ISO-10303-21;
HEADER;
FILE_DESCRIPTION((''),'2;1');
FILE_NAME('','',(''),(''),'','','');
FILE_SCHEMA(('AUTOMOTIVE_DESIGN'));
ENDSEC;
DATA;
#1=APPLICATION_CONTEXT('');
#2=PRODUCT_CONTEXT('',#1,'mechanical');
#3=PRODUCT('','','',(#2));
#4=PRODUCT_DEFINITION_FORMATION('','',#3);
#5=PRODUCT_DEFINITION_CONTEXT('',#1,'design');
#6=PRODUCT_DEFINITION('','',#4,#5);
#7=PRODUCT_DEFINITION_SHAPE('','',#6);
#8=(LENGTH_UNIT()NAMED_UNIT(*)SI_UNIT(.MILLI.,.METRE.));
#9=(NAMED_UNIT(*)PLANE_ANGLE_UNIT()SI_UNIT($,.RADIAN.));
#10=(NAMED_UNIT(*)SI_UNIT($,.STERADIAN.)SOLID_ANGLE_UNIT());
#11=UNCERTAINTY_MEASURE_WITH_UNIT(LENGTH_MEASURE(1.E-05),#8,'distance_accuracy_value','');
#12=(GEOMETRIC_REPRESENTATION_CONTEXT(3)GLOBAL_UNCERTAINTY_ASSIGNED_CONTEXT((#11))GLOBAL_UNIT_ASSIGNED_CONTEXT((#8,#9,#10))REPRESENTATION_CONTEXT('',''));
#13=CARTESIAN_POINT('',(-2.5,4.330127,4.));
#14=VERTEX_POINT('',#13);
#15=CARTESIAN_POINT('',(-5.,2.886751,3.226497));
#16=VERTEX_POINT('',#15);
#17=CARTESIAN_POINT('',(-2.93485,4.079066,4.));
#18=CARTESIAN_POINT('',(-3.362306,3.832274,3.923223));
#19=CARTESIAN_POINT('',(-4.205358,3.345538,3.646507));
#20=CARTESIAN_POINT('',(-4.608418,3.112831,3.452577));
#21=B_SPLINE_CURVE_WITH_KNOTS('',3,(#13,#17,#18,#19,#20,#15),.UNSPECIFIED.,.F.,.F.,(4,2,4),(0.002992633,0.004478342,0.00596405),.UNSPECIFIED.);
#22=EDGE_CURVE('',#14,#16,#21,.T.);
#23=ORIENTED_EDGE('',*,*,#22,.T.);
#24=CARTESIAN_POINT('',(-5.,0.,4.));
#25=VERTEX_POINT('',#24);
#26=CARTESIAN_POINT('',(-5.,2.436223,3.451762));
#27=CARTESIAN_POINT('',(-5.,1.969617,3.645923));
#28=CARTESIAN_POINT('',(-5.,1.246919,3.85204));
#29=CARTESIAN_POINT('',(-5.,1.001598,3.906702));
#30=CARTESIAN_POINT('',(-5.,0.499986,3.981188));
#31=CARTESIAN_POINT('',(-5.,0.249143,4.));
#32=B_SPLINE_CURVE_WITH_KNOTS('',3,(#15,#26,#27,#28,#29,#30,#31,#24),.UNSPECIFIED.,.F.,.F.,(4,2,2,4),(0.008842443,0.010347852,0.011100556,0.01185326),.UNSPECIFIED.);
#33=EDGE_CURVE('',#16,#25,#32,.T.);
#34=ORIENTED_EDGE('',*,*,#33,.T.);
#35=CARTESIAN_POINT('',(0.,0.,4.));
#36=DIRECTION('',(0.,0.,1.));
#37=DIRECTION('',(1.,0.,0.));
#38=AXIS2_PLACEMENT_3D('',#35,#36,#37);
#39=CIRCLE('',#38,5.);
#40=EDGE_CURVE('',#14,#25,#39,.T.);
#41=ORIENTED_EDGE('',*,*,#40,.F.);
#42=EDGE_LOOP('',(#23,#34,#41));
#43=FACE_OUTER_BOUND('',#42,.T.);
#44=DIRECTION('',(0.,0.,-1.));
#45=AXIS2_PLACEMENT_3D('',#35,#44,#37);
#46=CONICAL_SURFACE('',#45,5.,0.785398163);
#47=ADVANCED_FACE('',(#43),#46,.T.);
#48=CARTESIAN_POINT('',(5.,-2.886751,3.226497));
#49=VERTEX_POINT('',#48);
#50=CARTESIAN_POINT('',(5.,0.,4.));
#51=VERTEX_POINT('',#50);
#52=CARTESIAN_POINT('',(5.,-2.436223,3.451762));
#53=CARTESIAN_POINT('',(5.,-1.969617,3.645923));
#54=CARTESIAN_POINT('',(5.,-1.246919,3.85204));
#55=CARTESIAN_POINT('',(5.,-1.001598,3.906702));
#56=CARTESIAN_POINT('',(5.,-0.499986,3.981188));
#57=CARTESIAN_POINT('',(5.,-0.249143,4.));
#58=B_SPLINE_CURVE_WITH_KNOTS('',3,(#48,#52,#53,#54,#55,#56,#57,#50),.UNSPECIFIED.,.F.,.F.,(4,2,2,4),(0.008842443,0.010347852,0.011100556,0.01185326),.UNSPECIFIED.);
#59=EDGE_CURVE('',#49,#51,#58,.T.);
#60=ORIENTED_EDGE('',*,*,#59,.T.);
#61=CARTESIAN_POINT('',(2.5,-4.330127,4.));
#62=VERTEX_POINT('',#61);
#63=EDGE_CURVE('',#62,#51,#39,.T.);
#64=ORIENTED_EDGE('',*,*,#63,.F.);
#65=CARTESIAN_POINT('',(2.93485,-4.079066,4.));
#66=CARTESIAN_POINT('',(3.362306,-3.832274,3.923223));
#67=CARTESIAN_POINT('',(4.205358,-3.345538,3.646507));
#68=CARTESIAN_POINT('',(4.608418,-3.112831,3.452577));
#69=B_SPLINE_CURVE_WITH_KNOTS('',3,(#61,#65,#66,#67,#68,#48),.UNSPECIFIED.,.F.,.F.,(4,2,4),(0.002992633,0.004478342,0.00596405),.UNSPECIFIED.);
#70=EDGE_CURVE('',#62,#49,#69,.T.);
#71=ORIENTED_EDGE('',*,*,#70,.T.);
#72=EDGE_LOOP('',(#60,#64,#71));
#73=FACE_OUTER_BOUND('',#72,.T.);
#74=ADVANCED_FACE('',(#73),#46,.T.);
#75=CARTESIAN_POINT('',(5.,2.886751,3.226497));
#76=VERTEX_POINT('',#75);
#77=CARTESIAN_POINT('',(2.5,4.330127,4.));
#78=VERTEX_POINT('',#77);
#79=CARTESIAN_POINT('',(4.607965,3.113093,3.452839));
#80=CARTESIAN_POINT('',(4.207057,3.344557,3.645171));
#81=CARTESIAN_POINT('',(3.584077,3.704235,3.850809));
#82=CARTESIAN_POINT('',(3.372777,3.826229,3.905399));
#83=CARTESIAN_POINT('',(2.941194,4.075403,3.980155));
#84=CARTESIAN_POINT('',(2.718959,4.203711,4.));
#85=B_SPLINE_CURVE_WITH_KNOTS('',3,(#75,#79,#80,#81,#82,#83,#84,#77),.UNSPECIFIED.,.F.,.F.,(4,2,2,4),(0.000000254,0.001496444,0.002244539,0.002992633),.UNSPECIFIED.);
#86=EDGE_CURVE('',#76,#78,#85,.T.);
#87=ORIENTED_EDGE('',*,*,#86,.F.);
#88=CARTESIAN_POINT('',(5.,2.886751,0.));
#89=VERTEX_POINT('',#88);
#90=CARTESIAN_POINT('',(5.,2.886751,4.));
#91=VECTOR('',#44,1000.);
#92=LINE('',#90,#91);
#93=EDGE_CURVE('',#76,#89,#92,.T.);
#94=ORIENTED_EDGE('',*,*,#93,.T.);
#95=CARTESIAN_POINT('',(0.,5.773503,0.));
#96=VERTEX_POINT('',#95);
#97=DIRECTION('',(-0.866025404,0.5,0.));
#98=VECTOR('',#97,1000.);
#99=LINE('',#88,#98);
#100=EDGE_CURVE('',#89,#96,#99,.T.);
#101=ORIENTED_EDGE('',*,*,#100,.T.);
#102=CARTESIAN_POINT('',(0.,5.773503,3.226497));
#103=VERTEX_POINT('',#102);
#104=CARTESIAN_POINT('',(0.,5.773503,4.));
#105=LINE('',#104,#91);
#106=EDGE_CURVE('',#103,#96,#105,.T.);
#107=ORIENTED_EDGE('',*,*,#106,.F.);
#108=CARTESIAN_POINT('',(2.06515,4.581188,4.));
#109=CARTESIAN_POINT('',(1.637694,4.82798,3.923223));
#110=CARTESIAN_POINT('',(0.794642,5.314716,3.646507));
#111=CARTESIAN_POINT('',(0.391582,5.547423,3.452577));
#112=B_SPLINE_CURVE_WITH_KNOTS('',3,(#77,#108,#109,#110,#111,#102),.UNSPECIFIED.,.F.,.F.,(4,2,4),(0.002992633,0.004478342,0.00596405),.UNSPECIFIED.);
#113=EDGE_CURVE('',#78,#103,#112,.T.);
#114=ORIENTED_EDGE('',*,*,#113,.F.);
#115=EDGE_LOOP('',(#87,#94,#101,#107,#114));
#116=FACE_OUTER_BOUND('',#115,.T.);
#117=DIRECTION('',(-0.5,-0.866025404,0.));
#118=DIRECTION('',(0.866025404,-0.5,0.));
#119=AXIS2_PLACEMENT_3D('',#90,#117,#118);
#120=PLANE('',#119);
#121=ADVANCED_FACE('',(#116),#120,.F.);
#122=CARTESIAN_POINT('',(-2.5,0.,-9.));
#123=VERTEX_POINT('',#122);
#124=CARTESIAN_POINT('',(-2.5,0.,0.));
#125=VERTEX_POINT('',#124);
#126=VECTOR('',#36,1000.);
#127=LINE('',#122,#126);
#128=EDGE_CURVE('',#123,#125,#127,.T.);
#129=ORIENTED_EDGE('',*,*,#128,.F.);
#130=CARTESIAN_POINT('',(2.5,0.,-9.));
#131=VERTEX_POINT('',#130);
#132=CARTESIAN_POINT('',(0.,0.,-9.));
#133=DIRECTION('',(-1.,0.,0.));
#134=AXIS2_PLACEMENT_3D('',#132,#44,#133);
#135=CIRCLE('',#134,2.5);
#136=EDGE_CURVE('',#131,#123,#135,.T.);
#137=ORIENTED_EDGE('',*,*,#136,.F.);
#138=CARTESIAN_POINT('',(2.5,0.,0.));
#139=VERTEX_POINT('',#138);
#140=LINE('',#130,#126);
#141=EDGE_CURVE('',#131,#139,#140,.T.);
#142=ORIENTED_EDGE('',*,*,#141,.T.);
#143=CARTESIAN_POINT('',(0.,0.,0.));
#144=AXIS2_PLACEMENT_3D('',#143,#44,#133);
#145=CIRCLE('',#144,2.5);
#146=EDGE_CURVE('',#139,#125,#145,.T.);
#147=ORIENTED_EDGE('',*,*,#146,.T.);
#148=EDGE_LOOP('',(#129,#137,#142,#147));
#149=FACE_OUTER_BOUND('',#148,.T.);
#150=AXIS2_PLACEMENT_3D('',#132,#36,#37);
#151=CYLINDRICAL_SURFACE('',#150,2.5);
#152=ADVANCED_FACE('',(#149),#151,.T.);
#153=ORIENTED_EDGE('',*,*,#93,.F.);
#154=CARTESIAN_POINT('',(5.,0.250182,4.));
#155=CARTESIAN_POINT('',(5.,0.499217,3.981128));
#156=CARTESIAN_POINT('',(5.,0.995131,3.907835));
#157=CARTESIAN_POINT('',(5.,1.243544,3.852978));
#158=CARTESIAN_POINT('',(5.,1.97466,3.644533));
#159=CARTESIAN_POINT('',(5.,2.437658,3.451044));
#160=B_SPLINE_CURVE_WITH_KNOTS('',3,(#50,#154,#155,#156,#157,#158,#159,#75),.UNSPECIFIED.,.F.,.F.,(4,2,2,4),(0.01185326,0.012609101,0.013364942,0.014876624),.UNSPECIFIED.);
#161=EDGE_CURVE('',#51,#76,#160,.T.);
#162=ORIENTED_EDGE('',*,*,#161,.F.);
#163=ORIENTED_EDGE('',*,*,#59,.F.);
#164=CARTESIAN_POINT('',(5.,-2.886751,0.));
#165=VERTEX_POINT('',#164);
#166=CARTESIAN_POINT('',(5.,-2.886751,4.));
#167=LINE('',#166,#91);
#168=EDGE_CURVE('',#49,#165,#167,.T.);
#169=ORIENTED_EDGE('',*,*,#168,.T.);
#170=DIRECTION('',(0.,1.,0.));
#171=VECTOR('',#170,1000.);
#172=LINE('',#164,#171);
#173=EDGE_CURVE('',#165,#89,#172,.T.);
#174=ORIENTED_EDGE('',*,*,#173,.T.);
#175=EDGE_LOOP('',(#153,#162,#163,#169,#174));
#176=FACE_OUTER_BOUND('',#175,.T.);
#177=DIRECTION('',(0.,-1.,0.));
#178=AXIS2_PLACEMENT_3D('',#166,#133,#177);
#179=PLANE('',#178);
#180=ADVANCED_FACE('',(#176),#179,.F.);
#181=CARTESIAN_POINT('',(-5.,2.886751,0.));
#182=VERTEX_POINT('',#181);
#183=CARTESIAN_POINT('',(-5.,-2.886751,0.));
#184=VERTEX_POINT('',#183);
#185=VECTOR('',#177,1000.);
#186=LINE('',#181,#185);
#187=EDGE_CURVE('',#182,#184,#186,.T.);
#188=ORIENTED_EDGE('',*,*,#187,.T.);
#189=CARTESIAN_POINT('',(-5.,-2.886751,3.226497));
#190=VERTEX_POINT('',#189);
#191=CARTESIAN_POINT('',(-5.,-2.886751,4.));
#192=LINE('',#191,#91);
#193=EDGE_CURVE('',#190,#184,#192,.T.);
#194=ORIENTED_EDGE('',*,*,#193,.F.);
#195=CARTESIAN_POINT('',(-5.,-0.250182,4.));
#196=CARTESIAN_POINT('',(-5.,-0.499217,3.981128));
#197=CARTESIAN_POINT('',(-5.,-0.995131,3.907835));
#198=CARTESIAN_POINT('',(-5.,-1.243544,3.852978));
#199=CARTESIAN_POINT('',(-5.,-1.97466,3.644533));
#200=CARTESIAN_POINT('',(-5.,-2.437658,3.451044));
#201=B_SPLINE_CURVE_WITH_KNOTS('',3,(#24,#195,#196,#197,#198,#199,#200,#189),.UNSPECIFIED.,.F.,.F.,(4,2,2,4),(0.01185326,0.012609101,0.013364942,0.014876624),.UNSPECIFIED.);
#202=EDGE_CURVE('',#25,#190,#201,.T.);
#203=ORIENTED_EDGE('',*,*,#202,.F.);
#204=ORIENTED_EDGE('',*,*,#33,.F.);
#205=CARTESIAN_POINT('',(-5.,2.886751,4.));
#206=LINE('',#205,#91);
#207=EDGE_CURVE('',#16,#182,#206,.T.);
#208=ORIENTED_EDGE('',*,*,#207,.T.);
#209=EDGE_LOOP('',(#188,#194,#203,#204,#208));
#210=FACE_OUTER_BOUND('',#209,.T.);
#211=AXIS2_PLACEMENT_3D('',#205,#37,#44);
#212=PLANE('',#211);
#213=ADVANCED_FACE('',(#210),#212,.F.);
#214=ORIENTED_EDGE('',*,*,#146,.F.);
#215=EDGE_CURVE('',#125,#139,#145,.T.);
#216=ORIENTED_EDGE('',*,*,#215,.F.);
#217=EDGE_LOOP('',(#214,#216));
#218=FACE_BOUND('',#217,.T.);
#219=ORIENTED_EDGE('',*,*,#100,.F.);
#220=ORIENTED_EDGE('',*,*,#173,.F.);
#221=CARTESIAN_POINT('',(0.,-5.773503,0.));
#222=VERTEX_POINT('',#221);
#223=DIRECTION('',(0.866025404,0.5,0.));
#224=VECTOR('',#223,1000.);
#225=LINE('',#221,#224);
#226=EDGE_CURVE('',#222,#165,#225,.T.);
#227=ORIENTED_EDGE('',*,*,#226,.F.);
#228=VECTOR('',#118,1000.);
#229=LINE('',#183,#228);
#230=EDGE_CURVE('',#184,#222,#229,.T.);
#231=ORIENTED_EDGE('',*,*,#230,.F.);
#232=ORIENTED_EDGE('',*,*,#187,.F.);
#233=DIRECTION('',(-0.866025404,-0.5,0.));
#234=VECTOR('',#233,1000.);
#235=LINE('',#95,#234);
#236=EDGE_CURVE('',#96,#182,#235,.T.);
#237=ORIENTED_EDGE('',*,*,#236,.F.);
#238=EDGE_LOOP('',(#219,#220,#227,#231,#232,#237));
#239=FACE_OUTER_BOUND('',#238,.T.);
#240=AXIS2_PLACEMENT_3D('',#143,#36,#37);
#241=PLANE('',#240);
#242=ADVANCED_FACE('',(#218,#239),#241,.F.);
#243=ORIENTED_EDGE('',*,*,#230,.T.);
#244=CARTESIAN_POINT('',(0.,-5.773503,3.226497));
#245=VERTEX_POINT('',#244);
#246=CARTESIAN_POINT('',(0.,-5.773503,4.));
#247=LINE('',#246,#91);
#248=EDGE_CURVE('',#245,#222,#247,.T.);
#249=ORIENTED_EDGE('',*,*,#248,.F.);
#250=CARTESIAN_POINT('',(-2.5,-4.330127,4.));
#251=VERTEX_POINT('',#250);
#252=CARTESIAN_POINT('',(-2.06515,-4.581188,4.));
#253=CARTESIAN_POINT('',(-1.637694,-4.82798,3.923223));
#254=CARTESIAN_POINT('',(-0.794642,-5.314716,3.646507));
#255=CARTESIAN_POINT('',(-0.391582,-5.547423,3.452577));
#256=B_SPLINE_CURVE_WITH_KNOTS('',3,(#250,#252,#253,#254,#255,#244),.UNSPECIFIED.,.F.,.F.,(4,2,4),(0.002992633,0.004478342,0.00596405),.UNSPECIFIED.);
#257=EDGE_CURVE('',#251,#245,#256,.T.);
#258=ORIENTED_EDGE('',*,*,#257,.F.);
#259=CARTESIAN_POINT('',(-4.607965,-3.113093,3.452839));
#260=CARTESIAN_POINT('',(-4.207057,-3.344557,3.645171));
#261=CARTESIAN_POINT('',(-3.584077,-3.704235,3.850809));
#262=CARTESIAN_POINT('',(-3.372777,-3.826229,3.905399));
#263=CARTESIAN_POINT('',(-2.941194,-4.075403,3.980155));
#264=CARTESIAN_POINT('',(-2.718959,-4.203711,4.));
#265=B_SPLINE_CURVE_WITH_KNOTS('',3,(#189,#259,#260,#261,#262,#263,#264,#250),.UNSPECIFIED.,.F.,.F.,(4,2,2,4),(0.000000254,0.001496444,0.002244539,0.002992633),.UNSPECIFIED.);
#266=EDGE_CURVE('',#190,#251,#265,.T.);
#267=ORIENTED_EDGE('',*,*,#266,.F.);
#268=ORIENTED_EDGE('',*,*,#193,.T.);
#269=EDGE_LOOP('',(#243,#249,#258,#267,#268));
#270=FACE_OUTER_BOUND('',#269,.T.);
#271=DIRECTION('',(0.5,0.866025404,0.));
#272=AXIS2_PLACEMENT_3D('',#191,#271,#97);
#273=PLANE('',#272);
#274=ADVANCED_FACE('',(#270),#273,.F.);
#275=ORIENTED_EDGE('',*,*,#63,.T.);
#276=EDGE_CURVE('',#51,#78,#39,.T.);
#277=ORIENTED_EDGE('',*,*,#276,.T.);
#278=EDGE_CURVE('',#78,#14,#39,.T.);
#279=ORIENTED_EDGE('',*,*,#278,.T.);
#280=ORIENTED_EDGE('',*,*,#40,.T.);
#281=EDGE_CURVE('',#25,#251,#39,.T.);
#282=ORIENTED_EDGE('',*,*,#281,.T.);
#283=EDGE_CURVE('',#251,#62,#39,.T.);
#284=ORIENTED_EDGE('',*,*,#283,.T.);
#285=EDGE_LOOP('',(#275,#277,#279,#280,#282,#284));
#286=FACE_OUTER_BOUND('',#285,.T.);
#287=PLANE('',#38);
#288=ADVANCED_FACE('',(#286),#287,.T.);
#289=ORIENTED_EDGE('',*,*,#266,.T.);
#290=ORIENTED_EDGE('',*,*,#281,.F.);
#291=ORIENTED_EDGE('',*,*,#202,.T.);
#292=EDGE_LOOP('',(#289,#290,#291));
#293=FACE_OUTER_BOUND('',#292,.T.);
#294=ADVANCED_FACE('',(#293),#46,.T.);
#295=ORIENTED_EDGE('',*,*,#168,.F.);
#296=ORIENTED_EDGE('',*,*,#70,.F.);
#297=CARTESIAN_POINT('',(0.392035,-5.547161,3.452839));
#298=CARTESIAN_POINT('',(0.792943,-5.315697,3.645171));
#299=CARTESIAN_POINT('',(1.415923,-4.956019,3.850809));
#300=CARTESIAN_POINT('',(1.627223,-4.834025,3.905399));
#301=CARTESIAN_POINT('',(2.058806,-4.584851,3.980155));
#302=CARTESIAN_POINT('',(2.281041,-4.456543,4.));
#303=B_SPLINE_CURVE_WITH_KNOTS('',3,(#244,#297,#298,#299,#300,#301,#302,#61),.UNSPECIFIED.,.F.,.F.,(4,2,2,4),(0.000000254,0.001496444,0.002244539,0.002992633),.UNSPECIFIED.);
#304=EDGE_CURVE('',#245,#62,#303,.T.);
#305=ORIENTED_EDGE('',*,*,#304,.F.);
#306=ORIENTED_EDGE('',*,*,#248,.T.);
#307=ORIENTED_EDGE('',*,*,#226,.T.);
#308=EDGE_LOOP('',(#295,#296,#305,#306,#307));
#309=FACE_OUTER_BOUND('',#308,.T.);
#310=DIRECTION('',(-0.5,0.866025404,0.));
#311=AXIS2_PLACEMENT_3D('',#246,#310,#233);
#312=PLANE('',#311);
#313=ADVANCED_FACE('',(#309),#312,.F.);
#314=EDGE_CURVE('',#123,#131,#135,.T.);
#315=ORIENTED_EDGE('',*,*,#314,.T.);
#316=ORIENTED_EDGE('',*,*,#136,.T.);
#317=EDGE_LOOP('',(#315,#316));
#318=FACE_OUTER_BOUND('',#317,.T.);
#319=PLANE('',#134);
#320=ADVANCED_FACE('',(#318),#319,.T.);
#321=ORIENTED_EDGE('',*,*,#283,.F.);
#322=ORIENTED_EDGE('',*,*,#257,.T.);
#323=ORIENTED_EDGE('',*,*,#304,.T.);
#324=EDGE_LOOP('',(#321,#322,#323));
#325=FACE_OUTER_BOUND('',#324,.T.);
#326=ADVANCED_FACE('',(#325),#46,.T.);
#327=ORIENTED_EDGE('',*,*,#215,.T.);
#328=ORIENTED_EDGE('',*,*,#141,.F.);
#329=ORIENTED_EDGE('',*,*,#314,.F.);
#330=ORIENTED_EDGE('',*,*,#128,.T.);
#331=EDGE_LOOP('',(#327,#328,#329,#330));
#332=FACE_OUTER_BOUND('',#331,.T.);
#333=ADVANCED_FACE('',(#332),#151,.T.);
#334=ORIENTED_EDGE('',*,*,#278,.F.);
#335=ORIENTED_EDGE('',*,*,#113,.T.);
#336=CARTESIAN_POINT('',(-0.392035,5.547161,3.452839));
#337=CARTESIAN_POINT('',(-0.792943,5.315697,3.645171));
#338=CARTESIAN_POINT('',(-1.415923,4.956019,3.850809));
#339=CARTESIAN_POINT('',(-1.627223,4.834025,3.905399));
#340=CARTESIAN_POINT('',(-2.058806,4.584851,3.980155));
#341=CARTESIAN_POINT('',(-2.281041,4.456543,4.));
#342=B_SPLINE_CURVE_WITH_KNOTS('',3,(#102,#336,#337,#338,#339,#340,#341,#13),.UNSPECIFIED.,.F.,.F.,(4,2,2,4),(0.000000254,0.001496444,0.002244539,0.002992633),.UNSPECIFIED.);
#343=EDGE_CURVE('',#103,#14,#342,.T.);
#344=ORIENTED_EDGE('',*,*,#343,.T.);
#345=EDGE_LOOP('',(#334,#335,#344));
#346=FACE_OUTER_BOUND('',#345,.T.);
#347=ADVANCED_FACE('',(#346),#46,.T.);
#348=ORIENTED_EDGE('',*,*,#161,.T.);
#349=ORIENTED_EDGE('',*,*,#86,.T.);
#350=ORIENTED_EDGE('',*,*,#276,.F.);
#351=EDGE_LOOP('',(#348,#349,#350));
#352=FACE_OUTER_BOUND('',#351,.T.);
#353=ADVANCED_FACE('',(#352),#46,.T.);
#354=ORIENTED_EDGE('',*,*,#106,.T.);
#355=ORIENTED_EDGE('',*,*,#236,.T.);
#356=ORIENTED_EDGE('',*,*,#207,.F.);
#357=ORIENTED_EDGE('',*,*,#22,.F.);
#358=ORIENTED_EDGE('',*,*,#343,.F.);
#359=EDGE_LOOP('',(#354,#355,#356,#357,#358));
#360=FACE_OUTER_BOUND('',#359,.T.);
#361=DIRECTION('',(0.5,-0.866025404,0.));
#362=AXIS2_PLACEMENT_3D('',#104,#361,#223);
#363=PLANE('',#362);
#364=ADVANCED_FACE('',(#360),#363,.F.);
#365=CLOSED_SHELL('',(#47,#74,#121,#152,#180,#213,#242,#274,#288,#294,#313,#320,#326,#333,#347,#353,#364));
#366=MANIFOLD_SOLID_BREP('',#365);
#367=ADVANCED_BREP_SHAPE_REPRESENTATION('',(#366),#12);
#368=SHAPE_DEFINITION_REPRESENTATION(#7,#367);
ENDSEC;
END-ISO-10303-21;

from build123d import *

# Parameters (mm, degrees)
HEX_HEAD_DEPTH                 = 4
HEAD_CHAMFER_PROFILE_OUTSIDE_W = 23.158
HEAD_CHAMFER_PROFILE_OUTSIDE_H = 24.706
HEAD_CHAMFER_PROFILE_OUTSIDE_R = 5
HEAD_CHAMFER_45DEG_DEPTH       = 4
HEAD_CHAMFER_45DEG_DRAFT       = -45
SHANK_PROFILE_5_R              = 2.5
SHANK_5X9_DEPTH                = 9


with BuildPart() as part:
    # Hex Head Profile → Hex Head (new body)
    with BuildSketch(Plane.XY):
        Polygon((5, -2.886751346), (5, 2.886751346), (0, 5.773502692), (-5, 2.886751346), (-5, -2.886751346), (0, -5.773502692), align=None)
    extrude(amount=HEX_HEAD_DEPTH)


with BuildPart() as head_chamfer_45deg_tool:
    # Head Chamfer Profile outside → Head Chamfer 45deg (with draft: the straight prism first)
    with BuildSketch(Plane.XY.offset(4)):
        Rectangle(HEAD_CHAMFER_PROFILE_OUTSIDE_W, HEAD_CHAMFER_PROFILE_OUTSIDE_H)
        Circle(HEAD_CHAMFER_PROFILE_OUTSIDE_R, mode=Mode.SUBTRACT)
    extrude(amount=-HEAD_CHAMFER_45DEG_DEPTH)
    # Head Chamfer 45deg: the draft: its side faces are tilted about the plane it starts from
    head_chamfer_45deg_sides = [head_chamfer_45deg_tool.faces().sort_by_distance(p)[0] for p in [
        (0, -12.353, 2),
        (11.579, 0, 2),
        (0, 12.353, 2),
        (-11.579, 0, 2),
        (-5, 0, 2),
    ]]
    draft(head_chamfer_45deg_sides, Plane.XY.offset(4), HEAD_CHAMFER_45DEG_DRAFT)


with BuildPart() as part_1:
    add(part.part)

    # Head Chamfer 45deg: cut by head_chamfer_45deg_tool
    add(head_chamfer_45deg_tool.part, mode=Mode.SUBTRACT)

    # Shank Profile Ø5 → Shank Ø5x9 (add)
    with BuildSketch(Plane(origin=(0, 0, 0), x_dir=(-1, 0, 0), z_dir=(0, 0, -1))):
        Circle(SHANK_PROFILE_5_R)
    extrude(amount=SHANK_5X9_DEPTH)


solid = part_1.part
